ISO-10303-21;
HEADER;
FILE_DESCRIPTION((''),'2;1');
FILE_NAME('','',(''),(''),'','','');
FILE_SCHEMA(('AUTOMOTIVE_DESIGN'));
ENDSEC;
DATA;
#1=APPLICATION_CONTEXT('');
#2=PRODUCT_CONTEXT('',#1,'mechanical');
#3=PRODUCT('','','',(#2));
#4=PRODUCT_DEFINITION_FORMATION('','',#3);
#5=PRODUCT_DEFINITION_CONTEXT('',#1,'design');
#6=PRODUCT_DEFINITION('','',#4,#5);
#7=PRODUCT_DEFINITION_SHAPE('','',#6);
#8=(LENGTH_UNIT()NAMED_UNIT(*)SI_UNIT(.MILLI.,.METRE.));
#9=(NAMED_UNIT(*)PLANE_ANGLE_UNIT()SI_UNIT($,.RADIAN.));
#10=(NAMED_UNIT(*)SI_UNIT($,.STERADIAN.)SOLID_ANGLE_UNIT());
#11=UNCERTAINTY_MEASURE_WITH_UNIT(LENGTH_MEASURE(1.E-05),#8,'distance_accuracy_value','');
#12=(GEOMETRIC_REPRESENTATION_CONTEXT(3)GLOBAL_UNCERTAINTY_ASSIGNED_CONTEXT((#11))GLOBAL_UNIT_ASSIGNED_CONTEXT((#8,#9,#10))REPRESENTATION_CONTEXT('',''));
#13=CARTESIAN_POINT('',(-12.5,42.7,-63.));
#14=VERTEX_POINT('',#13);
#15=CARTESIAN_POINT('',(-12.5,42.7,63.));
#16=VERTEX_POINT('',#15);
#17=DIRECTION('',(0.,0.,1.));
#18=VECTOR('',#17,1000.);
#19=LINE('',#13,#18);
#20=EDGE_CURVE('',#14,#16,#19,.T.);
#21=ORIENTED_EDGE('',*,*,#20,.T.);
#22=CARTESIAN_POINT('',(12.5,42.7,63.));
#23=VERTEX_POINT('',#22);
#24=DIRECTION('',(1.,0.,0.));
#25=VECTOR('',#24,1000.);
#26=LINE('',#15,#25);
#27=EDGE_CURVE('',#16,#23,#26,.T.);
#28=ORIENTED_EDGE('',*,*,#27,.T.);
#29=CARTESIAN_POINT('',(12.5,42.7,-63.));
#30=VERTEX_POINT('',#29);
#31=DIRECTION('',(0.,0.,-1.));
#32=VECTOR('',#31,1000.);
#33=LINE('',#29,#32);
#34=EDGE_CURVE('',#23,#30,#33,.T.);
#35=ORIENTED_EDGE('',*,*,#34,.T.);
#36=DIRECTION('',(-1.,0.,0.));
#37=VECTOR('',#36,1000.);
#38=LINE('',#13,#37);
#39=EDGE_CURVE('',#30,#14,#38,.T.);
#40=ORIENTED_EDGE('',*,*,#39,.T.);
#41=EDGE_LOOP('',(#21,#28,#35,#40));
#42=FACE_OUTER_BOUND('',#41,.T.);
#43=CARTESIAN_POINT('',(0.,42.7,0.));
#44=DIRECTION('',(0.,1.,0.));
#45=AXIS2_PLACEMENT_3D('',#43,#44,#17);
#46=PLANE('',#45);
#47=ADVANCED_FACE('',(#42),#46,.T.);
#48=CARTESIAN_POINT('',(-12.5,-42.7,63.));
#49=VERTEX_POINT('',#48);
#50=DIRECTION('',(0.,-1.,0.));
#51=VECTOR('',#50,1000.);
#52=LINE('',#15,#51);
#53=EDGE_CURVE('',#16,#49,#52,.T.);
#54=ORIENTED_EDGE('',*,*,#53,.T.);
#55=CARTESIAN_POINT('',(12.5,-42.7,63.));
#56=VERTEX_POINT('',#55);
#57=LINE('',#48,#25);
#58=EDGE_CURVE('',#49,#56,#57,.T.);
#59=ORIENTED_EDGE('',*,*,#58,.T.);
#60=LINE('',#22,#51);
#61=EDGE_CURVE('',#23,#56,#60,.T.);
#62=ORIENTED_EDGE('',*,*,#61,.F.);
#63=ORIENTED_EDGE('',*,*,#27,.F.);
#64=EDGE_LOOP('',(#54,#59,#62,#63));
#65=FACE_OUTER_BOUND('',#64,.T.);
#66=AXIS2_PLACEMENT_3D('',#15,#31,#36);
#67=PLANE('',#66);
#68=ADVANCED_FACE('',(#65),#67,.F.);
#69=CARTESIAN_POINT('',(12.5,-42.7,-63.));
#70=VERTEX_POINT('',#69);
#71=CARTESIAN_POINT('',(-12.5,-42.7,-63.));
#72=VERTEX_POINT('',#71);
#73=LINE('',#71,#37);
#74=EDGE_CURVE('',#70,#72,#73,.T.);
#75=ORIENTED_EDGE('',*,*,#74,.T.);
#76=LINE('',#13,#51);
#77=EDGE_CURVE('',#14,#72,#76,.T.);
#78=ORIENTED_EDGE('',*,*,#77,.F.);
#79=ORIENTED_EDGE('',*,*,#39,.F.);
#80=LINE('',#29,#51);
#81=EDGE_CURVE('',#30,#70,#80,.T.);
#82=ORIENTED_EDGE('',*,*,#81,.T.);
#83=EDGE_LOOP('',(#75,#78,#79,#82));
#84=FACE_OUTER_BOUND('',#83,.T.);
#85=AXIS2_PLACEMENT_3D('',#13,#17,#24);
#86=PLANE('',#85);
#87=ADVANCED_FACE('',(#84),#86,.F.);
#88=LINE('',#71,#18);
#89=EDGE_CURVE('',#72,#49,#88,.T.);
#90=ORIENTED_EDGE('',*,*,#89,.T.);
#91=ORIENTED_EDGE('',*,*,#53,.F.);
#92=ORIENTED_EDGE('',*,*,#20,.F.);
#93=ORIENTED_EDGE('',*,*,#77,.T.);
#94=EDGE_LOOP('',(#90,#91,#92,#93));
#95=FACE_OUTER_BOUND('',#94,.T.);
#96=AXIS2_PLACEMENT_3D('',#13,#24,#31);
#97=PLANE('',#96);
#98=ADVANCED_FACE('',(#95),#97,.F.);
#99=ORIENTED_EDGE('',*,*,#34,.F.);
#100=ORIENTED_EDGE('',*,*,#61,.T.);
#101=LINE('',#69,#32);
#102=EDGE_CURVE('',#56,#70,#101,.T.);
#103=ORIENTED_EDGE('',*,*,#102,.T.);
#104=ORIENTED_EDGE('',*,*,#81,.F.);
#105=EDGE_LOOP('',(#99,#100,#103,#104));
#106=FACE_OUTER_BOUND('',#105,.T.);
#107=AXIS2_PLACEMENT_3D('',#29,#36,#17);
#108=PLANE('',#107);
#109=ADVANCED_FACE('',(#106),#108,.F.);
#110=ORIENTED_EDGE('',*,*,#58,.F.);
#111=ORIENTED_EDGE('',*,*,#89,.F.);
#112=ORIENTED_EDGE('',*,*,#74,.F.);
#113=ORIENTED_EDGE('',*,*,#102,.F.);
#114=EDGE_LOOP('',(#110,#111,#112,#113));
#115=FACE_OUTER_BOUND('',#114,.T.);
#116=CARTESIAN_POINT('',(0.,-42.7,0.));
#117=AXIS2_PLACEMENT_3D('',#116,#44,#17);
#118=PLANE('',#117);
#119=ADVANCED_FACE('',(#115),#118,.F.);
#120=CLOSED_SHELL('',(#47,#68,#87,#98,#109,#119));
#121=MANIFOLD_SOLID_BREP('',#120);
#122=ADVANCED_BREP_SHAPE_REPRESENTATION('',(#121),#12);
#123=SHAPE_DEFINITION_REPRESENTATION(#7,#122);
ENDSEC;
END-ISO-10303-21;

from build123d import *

# Parameters (mm, degrees)
SKETCH2_W           = 25
SKETCH2_H           = 126
BOSS_EXTRUDE1_DEPTH = 42.7


with BuildPart() as part:
    # Sketch2 → Boss-Extrude1 (new, symmetric)
    with BuildSketch(Plane(origin=(0, 0, 0), x_dir=(1, 0, 0), z_dir=(0, 1, 0))):
        Rectangle(SKETCH2_W, SKETCH2_H)
    extrude(amount=BOSS_EXTRUDE1_DEPTH, both=True)


solid = part.part
